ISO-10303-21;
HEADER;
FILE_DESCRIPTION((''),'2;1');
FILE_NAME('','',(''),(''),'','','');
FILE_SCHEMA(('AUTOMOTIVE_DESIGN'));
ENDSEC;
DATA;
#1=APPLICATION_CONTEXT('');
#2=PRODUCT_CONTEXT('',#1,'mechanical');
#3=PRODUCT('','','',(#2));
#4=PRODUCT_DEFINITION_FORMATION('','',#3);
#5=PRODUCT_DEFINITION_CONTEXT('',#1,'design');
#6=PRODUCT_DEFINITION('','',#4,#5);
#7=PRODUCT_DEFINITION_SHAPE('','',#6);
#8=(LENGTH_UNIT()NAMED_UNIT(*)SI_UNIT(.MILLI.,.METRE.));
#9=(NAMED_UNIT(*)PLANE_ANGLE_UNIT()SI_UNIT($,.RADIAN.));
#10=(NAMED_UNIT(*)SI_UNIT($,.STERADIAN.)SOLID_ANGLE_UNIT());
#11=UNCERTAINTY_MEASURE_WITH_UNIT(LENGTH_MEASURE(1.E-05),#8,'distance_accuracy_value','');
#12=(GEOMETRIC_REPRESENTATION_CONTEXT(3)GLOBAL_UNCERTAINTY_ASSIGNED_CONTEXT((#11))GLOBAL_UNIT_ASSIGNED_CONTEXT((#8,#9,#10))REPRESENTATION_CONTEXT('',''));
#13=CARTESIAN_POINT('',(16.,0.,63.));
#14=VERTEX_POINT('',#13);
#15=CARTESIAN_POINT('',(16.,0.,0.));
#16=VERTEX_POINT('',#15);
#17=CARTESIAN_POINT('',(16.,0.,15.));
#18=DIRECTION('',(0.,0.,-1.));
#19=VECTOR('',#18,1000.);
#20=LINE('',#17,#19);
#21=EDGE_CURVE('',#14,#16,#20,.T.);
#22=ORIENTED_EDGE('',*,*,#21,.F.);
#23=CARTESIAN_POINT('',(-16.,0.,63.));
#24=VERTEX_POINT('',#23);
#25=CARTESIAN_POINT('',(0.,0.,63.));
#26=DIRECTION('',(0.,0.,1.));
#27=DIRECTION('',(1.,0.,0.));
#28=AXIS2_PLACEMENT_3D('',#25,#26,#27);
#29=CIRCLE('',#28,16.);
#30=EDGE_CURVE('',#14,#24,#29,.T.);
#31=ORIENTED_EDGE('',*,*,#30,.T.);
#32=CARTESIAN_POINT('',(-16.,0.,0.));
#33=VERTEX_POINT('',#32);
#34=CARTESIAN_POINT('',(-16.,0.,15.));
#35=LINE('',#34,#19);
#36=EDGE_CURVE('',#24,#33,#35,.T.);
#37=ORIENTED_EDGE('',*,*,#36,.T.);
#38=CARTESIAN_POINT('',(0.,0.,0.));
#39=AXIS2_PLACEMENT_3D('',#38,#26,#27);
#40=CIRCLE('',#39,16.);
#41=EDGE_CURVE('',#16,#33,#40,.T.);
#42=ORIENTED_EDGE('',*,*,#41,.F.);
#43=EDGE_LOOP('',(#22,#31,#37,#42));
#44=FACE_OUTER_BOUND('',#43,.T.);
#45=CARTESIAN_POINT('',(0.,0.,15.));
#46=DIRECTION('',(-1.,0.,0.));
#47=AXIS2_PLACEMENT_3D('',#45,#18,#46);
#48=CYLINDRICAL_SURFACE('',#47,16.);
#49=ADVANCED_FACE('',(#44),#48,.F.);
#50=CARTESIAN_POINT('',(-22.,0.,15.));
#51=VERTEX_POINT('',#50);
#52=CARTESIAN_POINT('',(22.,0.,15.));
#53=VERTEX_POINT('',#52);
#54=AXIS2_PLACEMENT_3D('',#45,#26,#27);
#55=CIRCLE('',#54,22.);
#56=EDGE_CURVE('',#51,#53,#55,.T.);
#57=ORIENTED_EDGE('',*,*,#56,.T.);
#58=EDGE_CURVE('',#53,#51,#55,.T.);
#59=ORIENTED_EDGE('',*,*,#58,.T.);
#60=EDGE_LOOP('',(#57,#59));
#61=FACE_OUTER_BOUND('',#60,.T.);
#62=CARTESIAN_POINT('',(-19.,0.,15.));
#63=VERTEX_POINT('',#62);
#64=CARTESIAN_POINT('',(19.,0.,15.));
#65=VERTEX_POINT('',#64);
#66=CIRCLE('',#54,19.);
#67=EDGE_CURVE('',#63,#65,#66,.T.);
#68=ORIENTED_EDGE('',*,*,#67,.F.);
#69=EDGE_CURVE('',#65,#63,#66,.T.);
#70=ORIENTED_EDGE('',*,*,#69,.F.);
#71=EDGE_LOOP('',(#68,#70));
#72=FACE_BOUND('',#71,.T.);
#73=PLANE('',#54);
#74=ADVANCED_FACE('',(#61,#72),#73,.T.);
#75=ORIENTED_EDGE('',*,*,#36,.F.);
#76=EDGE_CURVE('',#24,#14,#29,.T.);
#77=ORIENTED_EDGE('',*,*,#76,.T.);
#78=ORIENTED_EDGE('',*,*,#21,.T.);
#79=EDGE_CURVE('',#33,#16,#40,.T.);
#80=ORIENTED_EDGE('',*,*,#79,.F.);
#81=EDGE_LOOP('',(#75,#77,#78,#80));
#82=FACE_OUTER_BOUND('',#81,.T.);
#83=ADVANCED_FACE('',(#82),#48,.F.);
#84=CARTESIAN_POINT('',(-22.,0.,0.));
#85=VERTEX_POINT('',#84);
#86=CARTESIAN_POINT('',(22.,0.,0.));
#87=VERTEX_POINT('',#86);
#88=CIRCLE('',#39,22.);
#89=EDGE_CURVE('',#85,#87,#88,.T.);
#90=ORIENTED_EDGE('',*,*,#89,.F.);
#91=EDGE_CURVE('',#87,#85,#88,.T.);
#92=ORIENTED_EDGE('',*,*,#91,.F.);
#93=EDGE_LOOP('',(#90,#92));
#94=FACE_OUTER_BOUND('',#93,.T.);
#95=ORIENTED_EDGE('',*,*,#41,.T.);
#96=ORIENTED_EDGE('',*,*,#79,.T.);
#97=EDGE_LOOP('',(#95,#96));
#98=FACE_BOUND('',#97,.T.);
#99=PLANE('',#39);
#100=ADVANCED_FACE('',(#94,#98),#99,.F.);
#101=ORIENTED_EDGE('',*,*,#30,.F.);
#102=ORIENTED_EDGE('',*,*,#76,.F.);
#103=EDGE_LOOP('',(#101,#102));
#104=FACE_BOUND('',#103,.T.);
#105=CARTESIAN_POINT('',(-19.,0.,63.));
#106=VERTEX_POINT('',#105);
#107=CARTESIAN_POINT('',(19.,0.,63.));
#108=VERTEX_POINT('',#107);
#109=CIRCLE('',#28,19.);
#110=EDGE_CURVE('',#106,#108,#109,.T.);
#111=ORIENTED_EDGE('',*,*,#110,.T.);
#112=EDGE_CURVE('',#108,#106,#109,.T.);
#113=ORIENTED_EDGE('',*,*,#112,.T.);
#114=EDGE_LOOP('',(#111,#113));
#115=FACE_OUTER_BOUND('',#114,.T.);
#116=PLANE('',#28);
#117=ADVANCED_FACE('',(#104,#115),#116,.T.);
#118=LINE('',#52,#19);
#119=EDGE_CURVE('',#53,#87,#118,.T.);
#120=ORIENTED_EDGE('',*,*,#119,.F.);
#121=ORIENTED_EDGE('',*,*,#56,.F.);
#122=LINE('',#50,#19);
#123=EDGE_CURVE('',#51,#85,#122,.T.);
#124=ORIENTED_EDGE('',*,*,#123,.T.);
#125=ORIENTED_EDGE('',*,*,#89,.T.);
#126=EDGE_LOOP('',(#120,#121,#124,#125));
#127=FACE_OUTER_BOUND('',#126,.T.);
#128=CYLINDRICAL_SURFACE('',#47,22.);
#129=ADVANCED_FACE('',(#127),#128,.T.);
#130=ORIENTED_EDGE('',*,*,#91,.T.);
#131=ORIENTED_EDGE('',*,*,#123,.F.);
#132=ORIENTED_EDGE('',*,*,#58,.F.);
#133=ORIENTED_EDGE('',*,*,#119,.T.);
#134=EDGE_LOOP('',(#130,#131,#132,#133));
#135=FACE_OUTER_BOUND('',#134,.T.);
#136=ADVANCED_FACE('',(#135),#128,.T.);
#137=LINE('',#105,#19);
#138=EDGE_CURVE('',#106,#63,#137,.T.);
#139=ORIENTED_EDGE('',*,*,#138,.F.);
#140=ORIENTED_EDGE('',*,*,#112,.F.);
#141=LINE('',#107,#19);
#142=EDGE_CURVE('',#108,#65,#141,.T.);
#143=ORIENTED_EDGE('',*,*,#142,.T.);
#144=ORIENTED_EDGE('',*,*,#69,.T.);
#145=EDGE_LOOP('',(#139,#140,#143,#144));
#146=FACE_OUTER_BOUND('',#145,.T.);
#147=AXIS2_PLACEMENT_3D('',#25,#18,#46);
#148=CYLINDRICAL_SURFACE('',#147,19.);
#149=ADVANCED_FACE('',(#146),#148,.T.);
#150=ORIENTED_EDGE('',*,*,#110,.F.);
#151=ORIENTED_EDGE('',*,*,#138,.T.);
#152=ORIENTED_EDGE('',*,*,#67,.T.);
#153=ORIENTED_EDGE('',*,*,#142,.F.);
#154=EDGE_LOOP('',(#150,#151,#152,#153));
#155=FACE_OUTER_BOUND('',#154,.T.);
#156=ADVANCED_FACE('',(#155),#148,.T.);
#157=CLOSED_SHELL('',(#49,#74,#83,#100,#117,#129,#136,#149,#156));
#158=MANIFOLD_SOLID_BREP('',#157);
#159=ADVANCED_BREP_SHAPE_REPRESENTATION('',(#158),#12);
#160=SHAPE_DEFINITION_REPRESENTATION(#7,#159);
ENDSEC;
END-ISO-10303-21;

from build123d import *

# Parameters (mm, degrees)
SKETCH_1_R      = 22
SKETCH_1_R_2    = 16
EXTRUDE_1_DEPTH = 15
SKETCH_2_R      = 19
SKETCH_2_R_2    = 16
EXTRUDE_2_DEPTH = 48


with BuildPart() as part:
    # 草图1 → 凸台-拉伸1 (new body)
    with BuildSketch(Plane.XY):
        Circle(SKETCH_1_R)
        Circle(SKETCH_1_R_2, mode=Mode.SUBTRACT)
    extrude(amount=EXTRUDE_1_DEPTH)

    # 草图2 → 凸台-拉伸2 (add)
    with BuildSketch(Plane.XY.offset(15)):
        Circle(SKETCH_2_R)
        Circle(SKETCH_2_R_2, mode=Mode.SUBTRACT)
    extrude(amount=EXTRUDE_2_DEPTH)


solid = part.part
